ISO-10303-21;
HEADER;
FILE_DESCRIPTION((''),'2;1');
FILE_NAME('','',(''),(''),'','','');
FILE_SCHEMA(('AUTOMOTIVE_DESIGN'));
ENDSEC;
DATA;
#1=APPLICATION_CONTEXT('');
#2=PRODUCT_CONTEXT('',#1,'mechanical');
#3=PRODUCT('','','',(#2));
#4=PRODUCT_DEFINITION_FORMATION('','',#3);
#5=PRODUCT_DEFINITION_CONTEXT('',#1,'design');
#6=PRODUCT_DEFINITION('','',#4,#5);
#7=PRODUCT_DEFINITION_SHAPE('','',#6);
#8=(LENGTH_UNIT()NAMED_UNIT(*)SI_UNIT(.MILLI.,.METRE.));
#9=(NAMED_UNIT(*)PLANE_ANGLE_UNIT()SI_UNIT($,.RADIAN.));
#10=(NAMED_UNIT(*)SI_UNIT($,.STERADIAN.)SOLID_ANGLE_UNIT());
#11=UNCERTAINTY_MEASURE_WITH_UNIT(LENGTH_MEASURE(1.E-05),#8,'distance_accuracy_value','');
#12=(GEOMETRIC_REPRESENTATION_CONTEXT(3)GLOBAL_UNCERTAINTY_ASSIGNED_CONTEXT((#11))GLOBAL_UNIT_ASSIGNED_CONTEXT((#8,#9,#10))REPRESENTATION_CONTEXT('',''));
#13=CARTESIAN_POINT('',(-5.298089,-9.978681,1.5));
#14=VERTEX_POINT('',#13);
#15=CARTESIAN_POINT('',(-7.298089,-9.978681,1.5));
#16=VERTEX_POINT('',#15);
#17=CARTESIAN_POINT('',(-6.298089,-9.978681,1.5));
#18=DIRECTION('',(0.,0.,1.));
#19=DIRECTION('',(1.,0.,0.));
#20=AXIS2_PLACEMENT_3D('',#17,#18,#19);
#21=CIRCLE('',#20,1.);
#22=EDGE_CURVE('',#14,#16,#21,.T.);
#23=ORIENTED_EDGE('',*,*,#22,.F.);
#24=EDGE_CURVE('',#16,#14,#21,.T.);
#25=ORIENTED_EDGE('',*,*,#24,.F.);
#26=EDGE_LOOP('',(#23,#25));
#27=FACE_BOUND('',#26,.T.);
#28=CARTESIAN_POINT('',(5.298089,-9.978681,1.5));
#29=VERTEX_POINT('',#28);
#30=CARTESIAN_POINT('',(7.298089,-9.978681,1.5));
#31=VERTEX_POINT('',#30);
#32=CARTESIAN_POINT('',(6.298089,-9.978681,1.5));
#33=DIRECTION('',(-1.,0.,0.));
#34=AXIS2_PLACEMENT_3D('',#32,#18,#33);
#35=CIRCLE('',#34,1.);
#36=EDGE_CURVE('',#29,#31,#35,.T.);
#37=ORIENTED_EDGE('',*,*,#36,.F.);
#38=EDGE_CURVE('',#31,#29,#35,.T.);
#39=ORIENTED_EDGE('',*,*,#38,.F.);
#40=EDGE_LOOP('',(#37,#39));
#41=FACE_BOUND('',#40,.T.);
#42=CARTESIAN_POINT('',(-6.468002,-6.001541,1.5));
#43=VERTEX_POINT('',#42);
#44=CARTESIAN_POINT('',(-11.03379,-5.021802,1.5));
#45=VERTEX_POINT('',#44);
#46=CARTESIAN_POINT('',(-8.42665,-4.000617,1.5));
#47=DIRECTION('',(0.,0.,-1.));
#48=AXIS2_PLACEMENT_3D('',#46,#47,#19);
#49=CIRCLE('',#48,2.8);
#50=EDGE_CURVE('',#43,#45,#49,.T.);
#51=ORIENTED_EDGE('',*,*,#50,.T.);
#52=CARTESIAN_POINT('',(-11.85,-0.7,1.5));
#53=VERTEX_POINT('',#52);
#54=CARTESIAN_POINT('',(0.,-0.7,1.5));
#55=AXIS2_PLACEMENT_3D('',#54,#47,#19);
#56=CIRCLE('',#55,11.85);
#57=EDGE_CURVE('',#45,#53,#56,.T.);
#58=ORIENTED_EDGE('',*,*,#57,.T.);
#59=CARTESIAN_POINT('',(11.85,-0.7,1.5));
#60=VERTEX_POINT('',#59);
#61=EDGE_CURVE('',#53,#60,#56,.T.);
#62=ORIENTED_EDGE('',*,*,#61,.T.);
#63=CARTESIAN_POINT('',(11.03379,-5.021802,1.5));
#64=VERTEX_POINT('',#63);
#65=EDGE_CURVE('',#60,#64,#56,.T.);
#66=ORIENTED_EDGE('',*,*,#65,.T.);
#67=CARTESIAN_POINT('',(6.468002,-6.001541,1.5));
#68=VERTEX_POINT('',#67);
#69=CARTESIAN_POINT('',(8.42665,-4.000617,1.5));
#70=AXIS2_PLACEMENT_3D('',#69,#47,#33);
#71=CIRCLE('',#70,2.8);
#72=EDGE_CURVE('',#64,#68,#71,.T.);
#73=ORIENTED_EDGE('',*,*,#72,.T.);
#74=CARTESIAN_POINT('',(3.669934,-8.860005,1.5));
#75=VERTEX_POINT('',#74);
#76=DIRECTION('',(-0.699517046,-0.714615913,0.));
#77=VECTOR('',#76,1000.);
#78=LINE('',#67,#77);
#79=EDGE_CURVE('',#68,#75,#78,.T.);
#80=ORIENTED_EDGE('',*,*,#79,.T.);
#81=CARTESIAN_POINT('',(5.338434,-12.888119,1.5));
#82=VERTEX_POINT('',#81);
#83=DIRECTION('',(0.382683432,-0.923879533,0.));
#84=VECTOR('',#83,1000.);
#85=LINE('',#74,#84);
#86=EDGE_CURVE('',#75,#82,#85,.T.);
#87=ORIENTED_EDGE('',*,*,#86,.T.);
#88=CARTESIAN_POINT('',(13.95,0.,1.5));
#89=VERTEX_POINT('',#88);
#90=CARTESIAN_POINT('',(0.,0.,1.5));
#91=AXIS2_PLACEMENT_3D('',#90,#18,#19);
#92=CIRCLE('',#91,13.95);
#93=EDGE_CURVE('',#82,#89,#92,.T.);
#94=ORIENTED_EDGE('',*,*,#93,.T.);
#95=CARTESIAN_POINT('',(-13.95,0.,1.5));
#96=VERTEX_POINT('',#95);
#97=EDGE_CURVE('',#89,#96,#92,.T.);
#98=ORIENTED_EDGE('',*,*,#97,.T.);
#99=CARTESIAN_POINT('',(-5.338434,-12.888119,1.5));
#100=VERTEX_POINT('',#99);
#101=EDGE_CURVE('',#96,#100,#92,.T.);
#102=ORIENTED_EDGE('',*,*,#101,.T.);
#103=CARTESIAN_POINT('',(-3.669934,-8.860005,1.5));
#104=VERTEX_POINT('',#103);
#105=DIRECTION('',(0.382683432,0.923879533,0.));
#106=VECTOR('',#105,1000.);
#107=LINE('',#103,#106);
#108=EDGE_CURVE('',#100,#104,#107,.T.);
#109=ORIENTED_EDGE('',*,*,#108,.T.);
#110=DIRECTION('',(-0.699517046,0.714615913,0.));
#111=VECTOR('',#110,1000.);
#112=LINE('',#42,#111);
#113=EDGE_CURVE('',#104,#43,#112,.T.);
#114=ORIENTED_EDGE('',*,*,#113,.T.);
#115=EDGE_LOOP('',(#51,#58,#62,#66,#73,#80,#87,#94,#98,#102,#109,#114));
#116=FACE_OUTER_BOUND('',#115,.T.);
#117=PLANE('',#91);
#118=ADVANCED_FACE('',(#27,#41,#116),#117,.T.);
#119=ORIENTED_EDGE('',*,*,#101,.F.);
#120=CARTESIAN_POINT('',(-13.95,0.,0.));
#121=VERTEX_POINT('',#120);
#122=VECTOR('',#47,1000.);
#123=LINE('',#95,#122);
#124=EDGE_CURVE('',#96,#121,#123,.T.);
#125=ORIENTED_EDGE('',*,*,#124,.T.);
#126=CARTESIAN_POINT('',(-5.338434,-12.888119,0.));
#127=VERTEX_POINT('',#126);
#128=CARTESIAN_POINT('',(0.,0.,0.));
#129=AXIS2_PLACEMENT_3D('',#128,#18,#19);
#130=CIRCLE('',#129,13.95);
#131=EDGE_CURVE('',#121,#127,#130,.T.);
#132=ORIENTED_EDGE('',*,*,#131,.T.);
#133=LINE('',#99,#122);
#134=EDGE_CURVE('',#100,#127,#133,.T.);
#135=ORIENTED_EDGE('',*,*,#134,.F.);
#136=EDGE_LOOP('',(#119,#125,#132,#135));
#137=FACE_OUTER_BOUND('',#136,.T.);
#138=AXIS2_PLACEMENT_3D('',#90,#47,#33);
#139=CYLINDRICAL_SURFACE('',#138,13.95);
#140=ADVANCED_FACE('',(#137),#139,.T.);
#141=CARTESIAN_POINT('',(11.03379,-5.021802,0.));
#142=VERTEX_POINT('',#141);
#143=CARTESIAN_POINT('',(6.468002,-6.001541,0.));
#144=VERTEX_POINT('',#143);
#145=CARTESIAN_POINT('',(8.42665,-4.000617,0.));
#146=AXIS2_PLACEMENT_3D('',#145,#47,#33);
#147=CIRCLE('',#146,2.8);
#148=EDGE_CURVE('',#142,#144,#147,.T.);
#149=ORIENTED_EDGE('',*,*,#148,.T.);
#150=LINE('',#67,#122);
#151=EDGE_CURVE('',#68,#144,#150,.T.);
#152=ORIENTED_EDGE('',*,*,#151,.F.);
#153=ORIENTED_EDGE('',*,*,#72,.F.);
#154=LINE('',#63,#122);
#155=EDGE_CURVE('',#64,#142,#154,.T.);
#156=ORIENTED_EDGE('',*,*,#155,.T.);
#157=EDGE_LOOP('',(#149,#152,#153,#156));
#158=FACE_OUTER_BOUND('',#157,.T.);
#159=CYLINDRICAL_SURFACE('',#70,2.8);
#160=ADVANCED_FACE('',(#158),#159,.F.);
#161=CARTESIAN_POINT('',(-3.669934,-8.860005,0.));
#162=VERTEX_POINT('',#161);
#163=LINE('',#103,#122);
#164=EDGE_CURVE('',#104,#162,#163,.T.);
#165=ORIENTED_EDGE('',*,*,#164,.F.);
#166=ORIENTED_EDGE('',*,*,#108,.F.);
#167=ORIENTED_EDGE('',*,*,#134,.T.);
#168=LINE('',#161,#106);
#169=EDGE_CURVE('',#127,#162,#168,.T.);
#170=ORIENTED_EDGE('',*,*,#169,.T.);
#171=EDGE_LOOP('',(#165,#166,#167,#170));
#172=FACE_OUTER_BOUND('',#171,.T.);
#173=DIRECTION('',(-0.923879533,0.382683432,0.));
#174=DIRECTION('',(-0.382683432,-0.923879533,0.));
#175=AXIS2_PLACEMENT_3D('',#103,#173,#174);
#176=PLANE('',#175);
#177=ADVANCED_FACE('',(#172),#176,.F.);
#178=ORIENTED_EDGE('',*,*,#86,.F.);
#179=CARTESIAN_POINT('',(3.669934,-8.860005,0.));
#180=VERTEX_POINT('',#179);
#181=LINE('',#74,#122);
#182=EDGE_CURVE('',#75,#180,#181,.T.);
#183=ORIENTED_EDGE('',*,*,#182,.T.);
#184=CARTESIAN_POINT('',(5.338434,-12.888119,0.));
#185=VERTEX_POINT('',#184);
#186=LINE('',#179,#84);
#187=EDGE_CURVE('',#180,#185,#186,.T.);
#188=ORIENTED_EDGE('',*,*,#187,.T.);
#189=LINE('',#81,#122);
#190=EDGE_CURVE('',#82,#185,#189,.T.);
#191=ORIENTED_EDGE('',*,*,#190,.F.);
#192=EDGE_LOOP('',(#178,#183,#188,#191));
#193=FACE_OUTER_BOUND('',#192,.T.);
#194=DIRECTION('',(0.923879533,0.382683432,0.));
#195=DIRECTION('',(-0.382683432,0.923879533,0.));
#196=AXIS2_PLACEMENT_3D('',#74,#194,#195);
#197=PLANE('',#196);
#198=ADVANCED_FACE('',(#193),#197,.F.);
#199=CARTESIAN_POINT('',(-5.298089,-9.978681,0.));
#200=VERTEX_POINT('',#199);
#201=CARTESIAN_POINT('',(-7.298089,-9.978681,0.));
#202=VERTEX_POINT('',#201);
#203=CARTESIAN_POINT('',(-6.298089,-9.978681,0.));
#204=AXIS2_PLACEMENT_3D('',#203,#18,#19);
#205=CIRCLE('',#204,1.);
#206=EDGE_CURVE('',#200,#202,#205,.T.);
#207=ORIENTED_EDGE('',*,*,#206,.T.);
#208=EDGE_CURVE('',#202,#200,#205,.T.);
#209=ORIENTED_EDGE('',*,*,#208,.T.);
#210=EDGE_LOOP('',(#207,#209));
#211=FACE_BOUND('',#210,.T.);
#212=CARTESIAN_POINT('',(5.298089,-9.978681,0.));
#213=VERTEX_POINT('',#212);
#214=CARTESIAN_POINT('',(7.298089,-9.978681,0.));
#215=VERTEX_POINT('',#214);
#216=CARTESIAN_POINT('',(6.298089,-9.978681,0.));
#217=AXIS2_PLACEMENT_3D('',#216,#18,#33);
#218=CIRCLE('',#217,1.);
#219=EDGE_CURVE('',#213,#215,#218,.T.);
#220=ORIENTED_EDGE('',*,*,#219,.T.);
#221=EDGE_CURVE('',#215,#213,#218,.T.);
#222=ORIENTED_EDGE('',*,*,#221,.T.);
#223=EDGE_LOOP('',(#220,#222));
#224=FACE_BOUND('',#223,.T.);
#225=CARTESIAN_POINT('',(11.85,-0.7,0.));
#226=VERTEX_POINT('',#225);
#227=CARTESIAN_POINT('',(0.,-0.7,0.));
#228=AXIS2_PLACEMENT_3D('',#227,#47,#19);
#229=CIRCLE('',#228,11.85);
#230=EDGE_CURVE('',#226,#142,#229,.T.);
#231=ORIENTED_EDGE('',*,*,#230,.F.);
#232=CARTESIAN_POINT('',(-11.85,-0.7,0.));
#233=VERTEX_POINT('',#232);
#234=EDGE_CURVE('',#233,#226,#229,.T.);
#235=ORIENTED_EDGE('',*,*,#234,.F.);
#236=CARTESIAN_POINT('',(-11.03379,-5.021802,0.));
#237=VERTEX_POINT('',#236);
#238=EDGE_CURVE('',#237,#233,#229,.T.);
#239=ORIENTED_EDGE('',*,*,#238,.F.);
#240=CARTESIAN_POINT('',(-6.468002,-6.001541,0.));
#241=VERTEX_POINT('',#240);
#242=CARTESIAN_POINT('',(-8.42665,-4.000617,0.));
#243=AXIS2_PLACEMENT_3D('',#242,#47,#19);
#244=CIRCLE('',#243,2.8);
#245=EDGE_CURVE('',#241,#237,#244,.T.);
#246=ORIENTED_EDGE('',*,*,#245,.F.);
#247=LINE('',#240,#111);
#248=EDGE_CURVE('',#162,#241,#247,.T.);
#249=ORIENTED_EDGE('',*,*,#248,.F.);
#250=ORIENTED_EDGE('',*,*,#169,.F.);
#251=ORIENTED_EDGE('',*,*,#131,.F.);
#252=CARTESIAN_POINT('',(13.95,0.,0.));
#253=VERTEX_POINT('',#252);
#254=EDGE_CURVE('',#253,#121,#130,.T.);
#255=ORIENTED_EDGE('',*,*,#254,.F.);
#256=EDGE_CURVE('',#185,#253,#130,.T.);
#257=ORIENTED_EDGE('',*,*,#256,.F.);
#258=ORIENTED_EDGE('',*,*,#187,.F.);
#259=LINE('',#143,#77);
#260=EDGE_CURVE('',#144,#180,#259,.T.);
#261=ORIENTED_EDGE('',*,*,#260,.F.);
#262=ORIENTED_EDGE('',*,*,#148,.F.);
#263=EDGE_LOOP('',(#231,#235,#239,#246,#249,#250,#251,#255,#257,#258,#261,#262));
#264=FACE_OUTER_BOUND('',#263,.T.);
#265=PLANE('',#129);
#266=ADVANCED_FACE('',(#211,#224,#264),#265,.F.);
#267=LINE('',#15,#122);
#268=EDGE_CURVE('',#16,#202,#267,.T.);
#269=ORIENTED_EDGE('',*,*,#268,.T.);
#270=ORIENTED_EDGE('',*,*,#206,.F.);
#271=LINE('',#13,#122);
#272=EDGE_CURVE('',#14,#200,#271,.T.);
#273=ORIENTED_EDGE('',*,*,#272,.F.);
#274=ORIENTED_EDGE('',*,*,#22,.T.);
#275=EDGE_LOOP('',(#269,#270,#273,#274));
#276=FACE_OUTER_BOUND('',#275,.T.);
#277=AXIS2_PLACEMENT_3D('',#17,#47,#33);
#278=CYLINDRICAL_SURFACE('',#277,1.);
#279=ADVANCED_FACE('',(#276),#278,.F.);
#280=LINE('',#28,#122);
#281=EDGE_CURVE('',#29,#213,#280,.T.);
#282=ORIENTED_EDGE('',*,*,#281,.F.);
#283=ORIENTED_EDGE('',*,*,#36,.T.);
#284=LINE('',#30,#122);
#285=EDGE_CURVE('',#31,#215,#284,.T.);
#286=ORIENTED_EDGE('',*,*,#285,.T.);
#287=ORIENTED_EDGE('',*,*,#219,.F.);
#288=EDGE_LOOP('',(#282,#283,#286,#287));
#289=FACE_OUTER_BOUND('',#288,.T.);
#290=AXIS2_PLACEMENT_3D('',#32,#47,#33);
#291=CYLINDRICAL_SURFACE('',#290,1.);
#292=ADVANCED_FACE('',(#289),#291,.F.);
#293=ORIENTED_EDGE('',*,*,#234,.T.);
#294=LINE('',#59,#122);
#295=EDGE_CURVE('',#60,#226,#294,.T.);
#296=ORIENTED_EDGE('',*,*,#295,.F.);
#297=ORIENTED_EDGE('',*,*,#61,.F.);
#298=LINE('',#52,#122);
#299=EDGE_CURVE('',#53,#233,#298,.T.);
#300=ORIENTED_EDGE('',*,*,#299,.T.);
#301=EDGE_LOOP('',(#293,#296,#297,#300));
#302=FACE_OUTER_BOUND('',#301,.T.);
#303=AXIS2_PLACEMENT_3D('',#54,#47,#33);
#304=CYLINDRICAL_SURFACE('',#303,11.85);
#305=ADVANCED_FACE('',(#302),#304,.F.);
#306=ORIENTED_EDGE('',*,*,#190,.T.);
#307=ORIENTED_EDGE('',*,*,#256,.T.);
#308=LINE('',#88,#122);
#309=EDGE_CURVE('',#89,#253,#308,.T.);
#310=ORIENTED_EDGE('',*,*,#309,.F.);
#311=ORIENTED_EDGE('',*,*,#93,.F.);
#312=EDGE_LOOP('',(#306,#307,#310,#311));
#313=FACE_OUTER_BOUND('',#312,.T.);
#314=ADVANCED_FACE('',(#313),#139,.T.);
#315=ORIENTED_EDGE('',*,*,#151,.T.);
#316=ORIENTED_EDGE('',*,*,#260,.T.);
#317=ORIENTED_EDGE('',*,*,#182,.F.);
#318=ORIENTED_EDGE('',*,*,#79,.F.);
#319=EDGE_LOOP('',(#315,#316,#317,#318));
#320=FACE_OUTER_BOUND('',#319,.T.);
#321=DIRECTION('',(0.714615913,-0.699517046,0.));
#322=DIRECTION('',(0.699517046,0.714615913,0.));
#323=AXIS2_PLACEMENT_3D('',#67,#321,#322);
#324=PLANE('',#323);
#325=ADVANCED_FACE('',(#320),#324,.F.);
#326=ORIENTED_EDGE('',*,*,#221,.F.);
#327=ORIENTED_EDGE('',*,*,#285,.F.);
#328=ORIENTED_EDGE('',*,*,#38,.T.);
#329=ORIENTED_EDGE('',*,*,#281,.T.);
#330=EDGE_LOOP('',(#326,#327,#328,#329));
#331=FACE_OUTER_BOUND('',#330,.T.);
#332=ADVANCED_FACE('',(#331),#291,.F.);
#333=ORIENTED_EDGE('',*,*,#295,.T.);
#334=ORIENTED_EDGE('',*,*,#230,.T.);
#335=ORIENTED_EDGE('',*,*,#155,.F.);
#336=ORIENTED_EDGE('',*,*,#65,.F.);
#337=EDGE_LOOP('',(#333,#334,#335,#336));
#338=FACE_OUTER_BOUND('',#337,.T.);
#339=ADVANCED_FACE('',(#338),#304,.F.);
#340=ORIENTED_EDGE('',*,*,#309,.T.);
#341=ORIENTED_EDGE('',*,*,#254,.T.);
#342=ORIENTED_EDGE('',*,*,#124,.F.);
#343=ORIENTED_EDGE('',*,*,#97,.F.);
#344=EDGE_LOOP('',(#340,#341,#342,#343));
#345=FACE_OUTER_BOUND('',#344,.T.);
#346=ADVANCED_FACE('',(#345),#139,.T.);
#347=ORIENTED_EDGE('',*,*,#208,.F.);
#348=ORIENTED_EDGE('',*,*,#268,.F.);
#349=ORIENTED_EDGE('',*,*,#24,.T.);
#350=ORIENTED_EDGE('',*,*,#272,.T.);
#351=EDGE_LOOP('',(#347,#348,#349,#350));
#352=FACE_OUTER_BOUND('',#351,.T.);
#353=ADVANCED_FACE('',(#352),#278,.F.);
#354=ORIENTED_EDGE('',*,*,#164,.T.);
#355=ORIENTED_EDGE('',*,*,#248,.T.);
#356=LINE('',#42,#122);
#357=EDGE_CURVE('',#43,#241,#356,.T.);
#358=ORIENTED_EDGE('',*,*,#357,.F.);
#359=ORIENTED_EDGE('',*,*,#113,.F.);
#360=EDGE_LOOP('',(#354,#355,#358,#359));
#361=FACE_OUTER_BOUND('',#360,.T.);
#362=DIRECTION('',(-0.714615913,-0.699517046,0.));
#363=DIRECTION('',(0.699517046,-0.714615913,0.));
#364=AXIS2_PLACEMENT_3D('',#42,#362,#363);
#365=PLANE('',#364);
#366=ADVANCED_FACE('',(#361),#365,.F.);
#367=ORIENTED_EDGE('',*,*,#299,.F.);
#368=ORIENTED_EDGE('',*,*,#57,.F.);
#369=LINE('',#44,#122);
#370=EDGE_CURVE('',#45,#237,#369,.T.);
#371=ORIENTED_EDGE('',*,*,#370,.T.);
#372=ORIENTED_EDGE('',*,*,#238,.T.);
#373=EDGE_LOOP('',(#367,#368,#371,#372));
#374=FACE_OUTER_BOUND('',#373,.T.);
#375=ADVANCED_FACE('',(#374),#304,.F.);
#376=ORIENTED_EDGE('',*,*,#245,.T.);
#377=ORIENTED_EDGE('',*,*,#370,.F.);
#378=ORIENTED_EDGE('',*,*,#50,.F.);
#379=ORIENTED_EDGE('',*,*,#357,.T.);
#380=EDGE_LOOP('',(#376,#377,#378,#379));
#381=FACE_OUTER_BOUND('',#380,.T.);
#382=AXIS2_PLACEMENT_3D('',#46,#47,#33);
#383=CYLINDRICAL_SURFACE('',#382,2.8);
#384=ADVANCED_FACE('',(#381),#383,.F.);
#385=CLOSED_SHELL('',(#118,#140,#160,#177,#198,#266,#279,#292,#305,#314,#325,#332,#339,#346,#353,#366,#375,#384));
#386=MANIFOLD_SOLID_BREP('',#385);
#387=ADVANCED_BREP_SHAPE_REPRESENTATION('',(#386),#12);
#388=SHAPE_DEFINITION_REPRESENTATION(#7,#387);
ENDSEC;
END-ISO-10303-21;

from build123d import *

# Parameters (mm, degrees)
SKETCH_1_R        = 1
EXTRUDE_952_DEPTH = 1.5


with BuildPart() as part:
    # 草图1 → Extrude 952 (new body)
    with BuildSketch(Plane.XY):
        with BuildLine():
            Line((-6.468002299, -6.001541065), (-3.669934116, -8.860004717))
            Line((-3.669934116, -8.860004717), (-5.338433881, -12.888119479))
            ThreePointArc((-5.338433881, -12.888119479), (0, 13.95), (5.338433881, -12.888119479))
            Line((5.338433881, -12.888119479), (3.669934116, -8.860004717))
            Line((3.669934116, -8.860004717), (6.468002299, -6.001541065))
            ThreePointArc((6.468002299, -6.001541065), (9.014108926, -6.738296556), (11.033790366, -5.021801727))
            ThreePointArc((11.033790366, -5.021801727), (0, 11.15), (-11.033790366, -5.021801727))
            ThreePointArc((-11.033790366, -5.021801727), (-9.014108926, -6.738296556), (-6.468002299, -6.001541065))
        make_face()
        with Locations((-6.298089329, -9.978680815)):
            Circle(SKETCH_1_R, mode=Mode.SUBTRACT)
        with Locations(Location((6.298089329, -9.978680815, 0), (0, 0, 180))):
            Circle(SKETCH_1_R, mode=Mode.SUBTRACT)
    extrude(amount=EXTRUDE_952_DEPTH)


solid = part.part
